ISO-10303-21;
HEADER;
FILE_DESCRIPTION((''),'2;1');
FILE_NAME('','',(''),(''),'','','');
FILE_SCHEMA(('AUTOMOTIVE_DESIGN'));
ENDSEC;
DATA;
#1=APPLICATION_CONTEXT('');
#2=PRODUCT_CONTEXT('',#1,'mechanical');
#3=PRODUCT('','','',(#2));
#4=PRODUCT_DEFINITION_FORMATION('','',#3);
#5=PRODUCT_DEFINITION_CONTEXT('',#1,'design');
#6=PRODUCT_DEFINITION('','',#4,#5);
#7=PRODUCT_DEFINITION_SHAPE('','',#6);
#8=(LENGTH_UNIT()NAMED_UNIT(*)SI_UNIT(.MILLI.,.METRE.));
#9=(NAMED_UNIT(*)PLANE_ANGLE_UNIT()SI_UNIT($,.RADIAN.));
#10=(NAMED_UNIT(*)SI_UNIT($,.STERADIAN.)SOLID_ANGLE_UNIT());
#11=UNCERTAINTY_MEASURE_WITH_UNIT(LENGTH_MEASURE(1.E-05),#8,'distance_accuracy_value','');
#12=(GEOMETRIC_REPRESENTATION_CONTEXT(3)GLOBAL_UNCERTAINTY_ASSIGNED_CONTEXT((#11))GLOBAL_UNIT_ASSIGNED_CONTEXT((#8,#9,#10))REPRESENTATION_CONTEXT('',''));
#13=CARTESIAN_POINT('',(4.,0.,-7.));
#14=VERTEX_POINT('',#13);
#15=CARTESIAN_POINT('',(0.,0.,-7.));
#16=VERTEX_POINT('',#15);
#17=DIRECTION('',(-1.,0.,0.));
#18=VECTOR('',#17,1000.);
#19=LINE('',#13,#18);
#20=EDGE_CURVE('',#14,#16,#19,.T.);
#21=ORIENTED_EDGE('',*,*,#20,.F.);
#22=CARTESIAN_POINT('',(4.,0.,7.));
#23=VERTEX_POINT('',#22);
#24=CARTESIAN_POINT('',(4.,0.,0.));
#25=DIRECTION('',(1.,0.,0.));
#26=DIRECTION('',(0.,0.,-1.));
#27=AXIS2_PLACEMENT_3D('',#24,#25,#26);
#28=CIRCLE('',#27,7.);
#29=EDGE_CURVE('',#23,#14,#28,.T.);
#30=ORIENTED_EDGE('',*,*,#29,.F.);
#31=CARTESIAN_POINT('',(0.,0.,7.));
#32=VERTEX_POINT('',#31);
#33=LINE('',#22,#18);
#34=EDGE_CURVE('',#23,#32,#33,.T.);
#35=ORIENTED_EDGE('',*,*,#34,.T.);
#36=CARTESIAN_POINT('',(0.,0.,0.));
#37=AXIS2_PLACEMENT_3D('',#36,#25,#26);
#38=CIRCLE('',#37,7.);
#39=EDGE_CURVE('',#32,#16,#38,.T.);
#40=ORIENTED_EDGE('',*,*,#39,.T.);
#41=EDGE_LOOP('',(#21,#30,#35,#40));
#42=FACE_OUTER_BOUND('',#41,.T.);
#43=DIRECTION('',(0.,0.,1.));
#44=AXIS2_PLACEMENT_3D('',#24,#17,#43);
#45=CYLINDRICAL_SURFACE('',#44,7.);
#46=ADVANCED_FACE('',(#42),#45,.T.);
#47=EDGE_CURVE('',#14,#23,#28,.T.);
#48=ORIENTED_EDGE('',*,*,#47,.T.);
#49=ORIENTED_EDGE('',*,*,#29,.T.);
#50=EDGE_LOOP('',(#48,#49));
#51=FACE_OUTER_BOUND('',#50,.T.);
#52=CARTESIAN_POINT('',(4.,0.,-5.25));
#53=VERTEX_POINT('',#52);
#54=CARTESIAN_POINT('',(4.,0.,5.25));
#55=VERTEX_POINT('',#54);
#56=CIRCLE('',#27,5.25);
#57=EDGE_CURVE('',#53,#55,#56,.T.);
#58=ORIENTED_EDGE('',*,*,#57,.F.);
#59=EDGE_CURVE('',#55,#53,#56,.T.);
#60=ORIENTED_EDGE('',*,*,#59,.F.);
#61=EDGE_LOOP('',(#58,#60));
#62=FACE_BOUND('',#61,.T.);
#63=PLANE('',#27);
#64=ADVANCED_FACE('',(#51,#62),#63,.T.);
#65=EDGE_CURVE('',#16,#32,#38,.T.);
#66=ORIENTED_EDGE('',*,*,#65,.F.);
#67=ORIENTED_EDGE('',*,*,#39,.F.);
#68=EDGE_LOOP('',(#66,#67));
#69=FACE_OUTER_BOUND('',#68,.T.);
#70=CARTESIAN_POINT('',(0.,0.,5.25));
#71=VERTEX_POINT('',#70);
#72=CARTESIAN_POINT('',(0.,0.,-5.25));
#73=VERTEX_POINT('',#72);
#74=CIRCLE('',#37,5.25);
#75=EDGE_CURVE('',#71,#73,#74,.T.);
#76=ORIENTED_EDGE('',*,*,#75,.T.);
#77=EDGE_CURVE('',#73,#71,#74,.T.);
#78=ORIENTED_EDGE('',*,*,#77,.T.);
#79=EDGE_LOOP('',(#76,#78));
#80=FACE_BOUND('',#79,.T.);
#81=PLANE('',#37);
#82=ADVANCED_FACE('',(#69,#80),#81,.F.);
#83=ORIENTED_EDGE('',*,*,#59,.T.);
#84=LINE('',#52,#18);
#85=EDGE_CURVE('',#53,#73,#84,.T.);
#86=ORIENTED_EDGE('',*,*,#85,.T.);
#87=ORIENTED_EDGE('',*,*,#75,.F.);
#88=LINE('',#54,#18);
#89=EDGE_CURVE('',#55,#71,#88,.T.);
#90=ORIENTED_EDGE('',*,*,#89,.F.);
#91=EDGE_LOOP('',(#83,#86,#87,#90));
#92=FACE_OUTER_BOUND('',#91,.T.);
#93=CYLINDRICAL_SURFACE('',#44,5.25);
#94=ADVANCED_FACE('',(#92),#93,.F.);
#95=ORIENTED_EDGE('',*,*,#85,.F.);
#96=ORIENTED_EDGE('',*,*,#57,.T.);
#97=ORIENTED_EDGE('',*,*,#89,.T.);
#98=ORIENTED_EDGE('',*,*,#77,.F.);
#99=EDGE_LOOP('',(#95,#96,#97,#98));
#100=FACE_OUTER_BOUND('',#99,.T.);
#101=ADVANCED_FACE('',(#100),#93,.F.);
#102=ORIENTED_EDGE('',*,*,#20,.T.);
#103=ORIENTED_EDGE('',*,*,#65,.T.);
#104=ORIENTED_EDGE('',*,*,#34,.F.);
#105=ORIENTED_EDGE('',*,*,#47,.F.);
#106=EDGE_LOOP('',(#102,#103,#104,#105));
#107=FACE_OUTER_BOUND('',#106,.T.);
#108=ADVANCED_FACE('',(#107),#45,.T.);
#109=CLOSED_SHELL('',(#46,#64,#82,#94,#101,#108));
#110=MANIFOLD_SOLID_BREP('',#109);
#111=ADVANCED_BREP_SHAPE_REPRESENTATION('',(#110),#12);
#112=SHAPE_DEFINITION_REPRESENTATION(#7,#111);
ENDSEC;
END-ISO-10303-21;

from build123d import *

# Parameters (mm, degrees)
SKETCH_1_R      = 7
SKETCH_1_R_2    = 5.25
EXTRUDE_1_DEPTH = 4


with BuildPart() as part:
    # 草图1 → 凸台-拉伸1 (new body)
    with BuildSketch(Plane(origin=(0, 0, 0), x_dir=(0, 0, -1), z_dir=(1, 0, 0))):
        Circle(SKETCH_1_R)
        Circle(SKETCH_1_R_2, mode=Mode.SUBTRACT)
    extrude(amount=EXTRUDE_1_DEPTH)


solid = part.part
